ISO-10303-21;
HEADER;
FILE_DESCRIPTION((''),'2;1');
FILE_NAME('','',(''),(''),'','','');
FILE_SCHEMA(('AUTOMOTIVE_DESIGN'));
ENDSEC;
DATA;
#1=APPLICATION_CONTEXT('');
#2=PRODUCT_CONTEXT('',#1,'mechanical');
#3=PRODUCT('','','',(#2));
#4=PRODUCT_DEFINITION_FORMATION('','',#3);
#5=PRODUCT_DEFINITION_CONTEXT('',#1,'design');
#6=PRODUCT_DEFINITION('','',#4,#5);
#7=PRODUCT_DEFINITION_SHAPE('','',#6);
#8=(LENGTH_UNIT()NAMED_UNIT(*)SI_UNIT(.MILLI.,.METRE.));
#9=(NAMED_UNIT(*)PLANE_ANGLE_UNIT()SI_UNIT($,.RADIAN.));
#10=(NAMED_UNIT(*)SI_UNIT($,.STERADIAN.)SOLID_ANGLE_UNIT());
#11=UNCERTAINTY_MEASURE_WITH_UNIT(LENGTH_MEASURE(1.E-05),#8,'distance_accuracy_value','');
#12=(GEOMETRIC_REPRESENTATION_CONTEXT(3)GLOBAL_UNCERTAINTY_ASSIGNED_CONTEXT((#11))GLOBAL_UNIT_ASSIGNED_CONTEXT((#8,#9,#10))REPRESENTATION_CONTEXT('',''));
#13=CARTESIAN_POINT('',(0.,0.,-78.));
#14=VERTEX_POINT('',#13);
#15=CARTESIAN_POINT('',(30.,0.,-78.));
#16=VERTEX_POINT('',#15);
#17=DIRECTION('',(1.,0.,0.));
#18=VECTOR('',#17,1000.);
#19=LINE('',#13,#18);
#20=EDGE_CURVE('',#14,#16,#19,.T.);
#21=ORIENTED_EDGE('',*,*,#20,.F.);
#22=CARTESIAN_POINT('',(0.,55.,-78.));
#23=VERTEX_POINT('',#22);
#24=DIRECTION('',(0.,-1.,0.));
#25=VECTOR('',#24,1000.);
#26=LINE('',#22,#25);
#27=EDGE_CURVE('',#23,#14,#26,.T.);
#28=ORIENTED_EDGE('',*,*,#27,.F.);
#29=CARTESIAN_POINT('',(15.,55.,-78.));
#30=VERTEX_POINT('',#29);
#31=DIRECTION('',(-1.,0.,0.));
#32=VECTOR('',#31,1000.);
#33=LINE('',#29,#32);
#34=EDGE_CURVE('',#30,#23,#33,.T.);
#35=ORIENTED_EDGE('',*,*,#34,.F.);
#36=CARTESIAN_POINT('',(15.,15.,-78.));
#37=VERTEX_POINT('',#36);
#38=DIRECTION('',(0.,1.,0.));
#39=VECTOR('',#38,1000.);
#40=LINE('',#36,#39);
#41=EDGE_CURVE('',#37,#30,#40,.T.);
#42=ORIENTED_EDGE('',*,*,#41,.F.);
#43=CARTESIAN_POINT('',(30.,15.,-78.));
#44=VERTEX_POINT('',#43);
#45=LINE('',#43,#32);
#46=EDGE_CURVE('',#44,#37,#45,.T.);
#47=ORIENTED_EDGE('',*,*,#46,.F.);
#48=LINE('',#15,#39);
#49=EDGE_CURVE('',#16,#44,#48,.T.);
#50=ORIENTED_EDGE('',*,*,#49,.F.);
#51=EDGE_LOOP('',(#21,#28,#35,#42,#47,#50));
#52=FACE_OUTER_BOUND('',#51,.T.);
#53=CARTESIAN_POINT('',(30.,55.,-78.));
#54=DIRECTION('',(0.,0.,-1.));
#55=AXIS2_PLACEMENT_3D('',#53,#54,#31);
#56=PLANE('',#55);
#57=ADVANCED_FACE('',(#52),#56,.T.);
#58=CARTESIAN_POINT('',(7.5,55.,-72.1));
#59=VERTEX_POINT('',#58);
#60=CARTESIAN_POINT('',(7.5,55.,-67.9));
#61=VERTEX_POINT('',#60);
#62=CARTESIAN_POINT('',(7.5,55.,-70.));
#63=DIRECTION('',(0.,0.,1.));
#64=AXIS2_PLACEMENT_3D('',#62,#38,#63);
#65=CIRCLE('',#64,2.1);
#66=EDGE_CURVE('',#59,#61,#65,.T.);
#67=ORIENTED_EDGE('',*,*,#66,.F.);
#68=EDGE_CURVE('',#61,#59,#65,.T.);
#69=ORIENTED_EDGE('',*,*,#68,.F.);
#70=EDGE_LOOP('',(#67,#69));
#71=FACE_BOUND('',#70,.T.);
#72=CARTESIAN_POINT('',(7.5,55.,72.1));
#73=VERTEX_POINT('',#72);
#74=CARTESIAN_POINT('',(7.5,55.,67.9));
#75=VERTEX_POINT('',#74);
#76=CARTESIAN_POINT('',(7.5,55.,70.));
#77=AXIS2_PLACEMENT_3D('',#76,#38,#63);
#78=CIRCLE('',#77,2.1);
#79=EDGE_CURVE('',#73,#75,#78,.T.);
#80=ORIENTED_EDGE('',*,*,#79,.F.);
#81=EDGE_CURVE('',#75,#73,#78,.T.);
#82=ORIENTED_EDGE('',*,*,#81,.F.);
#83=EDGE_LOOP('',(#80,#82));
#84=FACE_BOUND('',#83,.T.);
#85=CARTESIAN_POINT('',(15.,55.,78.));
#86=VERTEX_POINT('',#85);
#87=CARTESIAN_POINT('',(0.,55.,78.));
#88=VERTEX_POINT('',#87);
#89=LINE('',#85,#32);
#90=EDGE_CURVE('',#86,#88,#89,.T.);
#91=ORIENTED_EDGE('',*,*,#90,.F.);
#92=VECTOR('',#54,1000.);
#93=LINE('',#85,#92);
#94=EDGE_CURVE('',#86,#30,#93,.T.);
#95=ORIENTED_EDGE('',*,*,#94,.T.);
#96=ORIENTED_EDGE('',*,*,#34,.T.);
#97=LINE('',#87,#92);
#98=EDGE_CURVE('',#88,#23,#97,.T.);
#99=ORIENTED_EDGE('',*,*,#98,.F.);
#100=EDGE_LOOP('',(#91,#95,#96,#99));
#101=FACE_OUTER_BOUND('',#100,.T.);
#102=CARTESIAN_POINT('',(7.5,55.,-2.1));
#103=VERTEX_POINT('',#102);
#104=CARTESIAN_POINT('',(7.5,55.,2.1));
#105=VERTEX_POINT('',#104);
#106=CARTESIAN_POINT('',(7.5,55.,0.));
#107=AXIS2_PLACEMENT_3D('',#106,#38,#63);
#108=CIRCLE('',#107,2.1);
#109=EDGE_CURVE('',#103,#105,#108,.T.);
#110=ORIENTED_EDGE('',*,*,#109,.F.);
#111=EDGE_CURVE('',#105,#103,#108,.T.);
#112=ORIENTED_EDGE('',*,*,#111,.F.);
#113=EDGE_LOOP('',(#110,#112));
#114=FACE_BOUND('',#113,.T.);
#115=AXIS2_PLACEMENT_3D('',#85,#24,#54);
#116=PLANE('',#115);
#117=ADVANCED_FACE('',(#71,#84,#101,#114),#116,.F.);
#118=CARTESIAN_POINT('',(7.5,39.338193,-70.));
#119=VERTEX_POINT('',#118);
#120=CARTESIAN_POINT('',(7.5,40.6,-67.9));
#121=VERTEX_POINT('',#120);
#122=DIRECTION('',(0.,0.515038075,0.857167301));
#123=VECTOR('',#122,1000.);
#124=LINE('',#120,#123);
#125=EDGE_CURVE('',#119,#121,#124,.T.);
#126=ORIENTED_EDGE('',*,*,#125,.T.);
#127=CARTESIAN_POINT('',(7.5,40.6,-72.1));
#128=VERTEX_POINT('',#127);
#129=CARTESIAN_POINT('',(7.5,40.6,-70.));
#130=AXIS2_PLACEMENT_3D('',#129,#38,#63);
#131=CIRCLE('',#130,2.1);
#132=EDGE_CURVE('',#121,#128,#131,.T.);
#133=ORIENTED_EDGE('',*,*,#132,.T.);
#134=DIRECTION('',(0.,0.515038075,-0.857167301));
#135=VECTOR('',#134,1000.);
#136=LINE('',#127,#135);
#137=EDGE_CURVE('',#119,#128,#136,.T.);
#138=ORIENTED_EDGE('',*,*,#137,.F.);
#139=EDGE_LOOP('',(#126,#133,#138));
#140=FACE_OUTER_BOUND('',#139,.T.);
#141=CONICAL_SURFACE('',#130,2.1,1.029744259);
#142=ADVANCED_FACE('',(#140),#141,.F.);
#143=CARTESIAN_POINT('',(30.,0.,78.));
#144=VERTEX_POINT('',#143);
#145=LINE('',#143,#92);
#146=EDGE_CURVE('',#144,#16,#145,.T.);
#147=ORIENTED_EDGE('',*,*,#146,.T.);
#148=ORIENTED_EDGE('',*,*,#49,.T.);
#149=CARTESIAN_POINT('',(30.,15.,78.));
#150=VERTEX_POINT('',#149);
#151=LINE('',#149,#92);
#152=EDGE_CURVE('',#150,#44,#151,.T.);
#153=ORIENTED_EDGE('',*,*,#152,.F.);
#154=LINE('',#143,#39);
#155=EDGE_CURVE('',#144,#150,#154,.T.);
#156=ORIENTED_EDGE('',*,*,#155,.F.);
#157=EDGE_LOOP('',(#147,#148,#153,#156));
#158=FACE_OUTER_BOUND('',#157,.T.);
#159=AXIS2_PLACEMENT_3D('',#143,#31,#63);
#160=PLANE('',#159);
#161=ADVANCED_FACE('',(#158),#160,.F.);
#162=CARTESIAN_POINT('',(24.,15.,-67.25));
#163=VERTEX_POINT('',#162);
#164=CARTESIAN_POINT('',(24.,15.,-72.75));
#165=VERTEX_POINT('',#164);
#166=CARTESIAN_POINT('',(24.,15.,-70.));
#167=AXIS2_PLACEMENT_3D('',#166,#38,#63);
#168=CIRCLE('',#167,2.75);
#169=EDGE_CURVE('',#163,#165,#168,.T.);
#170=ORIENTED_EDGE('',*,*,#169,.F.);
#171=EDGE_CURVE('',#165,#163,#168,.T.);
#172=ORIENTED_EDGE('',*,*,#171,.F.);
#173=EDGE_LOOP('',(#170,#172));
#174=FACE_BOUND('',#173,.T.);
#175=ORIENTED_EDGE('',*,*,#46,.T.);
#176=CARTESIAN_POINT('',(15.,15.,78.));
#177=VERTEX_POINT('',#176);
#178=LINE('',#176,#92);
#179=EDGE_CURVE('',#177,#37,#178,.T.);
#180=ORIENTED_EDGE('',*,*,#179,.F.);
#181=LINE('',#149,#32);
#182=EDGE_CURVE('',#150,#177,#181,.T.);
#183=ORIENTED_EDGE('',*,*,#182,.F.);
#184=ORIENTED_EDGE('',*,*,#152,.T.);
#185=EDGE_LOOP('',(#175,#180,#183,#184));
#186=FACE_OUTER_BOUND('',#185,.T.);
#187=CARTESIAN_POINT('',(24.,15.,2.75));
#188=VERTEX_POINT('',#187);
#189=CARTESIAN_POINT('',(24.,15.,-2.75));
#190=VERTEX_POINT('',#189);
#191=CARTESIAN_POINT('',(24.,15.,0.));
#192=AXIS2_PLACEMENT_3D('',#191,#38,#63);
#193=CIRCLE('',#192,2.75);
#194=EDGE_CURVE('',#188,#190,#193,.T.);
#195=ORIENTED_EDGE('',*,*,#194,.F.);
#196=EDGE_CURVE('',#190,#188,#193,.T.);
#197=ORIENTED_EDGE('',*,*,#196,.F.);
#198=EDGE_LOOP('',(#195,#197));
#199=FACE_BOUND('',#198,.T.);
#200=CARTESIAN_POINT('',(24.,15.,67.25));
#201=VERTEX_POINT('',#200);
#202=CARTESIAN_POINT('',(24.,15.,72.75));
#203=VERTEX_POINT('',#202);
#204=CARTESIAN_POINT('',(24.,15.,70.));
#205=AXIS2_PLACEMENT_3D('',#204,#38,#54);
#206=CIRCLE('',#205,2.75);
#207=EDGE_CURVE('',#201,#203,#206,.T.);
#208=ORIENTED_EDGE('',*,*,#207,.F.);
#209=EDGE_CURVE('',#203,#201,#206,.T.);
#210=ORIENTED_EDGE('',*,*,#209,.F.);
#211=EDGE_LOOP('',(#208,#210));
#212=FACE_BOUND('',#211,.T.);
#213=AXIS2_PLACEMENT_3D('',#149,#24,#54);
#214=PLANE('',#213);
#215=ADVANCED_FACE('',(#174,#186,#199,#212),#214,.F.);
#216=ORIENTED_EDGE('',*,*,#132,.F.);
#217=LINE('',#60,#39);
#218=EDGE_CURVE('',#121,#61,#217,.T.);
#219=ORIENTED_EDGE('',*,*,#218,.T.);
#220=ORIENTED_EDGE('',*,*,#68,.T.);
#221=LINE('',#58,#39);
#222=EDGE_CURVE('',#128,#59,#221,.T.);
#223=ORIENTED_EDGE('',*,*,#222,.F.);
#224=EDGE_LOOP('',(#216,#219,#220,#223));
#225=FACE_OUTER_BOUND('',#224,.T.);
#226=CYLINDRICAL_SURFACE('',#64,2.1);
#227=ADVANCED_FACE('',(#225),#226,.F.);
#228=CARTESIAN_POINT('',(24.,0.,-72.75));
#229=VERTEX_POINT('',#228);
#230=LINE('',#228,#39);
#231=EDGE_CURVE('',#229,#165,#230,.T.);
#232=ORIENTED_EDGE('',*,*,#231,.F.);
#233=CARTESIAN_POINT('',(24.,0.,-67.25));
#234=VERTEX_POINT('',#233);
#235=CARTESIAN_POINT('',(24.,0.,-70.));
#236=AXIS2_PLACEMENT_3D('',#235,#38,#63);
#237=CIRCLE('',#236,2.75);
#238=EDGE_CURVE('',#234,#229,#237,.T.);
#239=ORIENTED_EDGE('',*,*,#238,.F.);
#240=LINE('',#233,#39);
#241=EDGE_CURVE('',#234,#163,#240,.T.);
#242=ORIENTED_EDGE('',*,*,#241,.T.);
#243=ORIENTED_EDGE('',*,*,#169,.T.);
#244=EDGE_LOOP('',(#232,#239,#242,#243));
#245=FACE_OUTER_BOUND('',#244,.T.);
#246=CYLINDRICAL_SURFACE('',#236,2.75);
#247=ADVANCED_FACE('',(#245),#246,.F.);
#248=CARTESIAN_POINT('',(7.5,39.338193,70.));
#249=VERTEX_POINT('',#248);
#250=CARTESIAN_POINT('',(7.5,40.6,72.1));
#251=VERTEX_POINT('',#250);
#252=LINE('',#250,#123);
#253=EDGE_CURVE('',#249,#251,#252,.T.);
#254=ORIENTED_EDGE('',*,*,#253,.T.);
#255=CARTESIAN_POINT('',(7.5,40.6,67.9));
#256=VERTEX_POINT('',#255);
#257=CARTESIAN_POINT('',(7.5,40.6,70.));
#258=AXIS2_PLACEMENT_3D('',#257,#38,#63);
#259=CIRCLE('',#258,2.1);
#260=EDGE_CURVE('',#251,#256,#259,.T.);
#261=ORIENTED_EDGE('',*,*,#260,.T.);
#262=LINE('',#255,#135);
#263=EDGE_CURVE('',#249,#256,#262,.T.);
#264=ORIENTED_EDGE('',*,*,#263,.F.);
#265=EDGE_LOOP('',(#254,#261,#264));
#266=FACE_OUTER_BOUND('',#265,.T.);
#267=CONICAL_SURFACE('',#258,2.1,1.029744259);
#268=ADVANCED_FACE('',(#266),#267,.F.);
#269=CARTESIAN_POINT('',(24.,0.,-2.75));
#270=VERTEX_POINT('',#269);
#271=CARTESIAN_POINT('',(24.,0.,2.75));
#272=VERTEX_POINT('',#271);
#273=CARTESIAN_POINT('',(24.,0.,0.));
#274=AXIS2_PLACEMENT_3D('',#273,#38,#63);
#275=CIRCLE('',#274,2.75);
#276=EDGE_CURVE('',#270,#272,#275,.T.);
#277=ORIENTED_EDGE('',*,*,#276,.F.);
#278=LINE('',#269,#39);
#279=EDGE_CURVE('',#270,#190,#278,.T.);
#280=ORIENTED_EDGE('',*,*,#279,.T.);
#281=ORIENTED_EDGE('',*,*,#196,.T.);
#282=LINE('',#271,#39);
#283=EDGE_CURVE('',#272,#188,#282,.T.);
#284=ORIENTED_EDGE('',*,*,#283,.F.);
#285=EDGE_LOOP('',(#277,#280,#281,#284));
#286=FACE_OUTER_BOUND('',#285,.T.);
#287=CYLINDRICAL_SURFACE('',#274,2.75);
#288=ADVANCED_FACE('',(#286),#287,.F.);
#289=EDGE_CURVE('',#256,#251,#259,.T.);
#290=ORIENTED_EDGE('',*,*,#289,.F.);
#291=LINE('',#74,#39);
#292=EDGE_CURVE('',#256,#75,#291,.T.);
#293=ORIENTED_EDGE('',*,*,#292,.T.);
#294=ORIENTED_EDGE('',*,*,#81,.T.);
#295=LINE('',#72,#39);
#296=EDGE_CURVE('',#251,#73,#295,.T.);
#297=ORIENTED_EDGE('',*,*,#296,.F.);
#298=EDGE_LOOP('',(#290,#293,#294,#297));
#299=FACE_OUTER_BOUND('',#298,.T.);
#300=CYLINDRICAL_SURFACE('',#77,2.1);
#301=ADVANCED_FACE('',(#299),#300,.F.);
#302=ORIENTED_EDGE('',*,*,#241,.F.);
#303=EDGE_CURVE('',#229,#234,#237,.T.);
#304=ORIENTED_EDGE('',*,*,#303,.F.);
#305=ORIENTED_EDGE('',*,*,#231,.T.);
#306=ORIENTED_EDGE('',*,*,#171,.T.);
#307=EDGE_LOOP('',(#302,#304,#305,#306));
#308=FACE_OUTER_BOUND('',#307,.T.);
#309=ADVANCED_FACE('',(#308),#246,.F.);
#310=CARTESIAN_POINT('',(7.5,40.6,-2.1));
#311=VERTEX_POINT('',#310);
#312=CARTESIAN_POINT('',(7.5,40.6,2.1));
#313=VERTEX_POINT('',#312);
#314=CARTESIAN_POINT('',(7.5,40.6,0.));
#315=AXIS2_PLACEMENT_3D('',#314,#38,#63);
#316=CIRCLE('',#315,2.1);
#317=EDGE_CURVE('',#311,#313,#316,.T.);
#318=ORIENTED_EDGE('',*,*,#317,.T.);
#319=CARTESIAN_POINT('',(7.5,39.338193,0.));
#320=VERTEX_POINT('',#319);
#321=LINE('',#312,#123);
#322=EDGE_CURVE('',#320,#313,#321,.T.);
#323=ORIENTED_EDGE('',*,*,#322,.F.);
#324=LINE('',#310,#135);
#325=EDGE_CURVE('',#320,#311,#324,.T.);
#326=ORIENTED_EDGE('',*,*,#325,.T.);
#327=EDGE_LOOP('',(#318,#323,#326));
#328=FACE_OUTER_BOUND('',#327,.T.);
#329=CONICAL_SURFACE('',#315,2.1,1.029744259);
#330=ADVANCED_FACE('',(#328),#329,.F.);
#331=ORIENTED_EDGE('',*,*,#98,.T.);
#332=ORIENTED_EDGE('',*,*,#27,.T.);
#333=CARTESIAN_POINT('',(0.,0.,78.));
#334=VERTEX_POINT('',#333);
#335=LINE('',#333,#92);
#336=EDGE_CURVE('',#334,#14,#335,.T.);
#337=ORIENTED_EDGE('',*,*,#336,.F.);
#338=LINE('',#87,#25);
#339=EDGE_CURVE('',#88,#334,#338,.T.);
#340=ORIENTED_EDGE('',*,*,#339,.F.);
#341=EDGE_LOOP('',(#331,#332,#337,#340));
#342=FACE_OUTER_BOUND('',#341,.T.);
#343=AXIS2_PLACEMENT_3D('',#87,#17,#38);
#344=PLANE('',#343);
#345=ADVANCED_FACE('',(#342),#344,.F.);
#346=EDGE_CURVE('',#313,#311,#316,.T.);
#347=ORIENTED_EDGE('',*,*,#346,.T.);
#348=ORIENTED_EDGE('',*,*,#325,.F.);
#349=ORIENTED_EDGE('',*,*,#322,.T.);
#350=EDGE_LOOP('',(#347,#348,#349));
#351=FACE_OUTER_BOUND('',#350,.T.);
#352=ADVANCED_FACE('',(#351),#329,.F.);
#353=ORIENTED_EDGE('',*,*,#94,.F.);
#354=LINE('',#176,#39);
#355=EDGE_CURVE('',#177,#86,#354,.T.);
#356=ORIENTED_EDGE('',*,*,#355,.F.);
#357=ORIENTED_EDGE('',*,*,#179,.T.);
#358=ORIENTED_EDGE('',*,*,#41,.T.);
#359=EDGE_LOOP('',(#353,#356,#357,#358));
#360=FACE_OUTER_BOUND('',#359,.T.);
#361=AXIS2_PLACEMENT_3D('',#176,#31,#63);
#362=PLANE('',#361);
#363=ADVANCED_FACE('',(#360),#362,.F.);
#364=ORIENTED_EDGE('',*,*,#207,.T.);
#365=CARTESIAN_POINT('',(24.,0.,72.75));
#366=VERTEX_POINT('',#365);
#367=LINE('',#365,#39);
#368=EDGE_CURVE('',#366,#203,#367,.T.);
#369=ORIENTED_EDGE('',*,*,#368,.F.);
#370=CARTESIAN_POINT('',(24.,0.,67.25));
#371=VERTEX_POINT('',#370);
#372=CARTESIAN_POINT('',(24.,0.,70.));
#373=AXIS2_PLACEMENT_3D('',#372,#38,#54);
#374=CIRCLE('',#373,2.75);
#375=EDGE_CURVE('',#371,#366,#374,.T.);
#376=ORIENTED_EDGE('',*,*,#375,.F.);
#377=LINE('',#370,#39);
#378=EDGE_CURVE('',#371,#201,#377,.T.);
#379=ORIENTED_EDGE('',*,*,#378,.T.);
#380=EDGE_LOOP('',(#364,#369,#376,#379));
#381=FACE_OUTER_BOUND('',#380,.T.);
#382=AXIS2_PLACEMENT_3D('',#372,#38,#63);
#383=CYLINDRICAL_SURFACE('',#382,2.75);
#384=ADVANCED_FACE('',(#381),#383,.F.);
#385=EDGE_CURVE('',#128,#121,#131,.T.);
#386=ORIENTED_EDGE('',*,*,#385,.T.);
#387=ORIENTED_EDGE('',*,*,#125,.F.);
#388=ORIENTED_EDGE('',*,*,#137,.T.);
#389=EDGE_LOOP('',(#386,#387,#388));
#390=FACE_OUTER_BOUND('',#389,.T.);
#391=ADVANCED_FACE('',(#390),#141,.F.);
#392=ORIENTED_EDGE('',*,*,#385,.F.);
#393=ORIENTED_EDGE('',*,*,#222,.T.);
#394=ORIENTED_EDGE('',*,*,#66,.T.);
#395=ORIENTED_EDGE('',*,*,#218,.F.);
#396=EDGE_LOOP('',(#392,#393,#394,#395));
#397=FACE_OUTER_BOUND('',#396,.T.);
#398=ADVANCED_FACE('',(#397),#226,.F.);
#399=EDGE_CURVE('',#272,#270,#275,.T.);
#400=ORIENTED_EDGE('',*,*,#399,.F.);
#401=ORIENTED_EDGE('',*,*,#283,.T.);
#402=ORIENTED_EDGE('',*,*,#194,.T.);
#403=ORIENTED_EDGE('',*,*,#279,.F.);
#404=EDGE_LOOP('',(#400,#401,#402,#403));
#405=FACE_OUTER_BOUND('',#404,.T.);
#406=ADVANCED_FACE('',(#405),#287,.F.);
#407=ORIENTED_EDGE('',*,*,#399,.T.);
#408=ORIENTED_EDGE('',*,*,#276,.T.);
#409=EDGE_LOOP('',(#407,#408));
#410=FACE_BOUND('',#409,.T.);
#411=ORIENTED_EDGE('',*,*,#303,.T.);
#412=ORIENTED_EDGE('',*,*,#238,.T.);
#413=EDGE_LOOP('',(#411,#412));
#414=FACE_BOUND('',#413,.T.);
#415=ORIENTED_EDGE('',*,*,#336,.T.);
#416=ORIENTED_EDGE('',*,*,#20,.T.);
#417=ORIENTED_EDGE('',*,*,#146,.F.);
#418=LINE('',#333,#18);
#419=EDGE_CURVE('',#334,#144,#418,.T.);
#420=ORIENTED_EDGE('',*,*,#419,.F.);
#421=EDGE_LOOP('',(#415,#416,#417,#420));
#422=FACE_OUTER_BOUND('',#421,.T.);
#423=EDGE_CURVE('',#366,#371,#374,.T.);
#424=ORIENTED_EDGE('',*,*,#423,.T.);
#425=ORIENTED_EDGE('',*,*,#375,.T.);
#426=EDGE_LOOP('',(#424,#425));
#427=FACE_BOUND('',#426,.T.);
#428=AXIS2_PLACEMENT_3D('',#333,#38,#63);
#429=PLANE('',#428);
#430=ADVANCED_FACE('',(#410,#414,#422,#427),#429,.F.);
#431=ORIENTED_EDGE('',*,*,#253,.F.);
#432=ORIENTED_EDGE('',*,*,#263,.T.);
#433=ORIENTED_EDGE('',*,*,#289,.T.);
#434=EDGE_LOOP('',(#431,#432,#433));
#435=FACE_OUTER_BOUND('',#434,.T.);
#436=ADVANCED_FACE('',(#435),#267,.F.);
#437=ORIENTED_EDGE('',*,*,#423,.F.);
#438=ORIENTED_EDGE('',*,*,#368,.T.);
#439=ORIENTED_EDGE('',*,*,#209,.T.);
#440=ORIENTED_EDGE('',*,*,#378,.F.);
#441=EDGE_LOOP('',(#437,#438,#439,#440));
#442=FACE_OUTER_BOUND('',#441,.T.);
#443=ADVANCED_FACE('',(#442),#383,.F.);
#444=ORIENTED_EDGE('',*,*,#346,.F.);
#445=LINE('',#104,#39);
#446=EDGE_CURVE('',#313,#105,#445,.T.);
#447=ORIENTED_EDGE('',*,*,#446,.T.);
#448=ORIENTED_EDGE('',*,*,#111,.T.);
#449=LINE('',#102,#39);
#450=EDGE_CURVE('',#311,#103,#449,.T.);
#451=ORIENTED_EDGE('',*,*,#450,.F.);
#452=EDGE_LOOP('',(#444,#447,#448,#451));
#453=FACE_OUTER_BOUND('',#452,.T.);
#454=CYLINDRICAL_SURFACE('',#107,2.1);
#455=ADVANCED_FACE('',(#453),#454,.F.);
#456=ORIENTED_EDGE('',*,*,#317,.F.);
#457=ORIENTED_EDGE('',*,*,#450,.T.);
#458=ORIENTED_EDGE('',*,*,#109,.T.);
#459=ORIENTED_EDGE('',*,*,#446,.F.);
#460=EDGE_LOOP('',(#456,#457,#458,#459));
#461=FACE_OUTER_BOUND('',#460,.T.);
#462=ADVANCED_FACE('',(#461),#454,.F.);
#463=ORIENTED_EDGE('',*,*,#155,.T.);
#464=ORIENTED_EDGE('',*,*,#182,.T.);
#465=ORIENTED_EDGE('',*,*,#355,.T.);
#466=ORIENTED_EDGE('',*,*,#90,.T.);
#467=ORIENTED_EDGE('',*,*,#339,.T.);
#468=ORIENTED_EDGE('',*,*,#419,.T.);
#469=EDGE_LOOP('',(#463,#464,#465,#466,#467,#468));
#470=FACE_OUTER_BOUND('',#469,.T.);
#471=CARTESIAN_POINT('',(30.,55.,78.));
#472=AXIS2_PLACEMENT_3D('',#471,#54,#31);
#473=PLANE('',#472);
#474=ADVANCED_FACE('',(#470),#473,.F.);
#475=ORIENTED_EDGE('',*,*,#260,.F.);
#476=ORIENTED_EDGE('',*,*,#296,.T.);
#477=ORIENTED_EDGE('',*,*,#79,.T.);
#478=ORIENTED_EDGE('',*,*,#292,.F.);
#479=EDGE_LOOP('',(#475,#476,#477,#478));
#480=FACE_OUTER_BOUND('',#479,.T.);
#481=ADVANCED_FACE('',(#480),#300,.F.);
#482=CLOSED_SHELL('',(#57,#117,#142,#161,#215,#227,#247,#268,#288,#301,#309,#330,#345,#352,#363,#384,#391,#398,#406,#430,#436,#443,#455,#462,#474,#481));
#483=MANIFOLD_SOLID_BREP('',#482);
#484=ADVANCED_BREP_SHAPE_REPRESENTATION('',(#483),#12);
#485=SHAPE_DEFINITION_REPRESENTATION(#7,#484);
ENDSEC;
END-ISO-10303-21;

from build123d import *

# Parameters (mm, degrees)
EXTRUDE1_DEPTH        = 78
M5_TAPPED_HOLE1_D     = 4.2
M5_TAPPED_HOLE1_DEPTH = 14.4
M5_TAPPED_HOLE1_TIP   = 1.2618073
SKETCH3_R             = 2.75
CUT_EXTRUDE1_DEPTH    = 93.649878575


with BuildPart() as part:
    # Sketch1 → Extrude1 (new, symmetric)
    with BuildSketch(Plane.XY):
        Polygon((0, 55), (0, 0), (30, 0), (30, 15), (15, 15), (15, 55), align=None)
    extrude(amount=EXTRUDE1_DEPTH, both=True)

    # M5 Tapped Hole1
    with Locations(Plane(origin=(7.5, 55, 0), x_dir=(0, 0, 1), z_dir=(0, 1, 0))):
        with Locations((0, 0), (-70, 0), (70, 0)):
            Hole(M5_TAPPED_HOLE1_D / 2, depth=M5_TAPPED_HOLE1_DEPTH)
            with Locations((0, 0, -(M5_TAPPED_HOLE1_DEPTH + M5_TAPPED_HOLE1_TIP / 2))):  # 118° drill point
                Cone(0, M5_TAPPED_HOLE1_D / 2, M5_TAPPED_HOLE1_TIP, mode=Mode.SUBTRACT)

    # Sketch3 → Cut-Extrude1 (cut, through all)
    with BuildSketch(Plane(origin=(0, 15, 0), x_dir=(1, 0, 0), z_dir=(0, 1, 0))):
        with Locations(Location((24, 0, 0), (0, 0, 270))):
            Circle(SKETCH3_R)
        with Locations(Location((24, 70, 0), (0, 0, 270))):
            Circle(SKETCH3_R)
        with Locations(Location((24, -70, 0), (0, 0, 90))):
            Circle(SKETCH3_R)
    extrude(amount=-CUT_EXTRUDE1_DEPTH, mode=Mode.SUBTRACT)


solid = part.part
